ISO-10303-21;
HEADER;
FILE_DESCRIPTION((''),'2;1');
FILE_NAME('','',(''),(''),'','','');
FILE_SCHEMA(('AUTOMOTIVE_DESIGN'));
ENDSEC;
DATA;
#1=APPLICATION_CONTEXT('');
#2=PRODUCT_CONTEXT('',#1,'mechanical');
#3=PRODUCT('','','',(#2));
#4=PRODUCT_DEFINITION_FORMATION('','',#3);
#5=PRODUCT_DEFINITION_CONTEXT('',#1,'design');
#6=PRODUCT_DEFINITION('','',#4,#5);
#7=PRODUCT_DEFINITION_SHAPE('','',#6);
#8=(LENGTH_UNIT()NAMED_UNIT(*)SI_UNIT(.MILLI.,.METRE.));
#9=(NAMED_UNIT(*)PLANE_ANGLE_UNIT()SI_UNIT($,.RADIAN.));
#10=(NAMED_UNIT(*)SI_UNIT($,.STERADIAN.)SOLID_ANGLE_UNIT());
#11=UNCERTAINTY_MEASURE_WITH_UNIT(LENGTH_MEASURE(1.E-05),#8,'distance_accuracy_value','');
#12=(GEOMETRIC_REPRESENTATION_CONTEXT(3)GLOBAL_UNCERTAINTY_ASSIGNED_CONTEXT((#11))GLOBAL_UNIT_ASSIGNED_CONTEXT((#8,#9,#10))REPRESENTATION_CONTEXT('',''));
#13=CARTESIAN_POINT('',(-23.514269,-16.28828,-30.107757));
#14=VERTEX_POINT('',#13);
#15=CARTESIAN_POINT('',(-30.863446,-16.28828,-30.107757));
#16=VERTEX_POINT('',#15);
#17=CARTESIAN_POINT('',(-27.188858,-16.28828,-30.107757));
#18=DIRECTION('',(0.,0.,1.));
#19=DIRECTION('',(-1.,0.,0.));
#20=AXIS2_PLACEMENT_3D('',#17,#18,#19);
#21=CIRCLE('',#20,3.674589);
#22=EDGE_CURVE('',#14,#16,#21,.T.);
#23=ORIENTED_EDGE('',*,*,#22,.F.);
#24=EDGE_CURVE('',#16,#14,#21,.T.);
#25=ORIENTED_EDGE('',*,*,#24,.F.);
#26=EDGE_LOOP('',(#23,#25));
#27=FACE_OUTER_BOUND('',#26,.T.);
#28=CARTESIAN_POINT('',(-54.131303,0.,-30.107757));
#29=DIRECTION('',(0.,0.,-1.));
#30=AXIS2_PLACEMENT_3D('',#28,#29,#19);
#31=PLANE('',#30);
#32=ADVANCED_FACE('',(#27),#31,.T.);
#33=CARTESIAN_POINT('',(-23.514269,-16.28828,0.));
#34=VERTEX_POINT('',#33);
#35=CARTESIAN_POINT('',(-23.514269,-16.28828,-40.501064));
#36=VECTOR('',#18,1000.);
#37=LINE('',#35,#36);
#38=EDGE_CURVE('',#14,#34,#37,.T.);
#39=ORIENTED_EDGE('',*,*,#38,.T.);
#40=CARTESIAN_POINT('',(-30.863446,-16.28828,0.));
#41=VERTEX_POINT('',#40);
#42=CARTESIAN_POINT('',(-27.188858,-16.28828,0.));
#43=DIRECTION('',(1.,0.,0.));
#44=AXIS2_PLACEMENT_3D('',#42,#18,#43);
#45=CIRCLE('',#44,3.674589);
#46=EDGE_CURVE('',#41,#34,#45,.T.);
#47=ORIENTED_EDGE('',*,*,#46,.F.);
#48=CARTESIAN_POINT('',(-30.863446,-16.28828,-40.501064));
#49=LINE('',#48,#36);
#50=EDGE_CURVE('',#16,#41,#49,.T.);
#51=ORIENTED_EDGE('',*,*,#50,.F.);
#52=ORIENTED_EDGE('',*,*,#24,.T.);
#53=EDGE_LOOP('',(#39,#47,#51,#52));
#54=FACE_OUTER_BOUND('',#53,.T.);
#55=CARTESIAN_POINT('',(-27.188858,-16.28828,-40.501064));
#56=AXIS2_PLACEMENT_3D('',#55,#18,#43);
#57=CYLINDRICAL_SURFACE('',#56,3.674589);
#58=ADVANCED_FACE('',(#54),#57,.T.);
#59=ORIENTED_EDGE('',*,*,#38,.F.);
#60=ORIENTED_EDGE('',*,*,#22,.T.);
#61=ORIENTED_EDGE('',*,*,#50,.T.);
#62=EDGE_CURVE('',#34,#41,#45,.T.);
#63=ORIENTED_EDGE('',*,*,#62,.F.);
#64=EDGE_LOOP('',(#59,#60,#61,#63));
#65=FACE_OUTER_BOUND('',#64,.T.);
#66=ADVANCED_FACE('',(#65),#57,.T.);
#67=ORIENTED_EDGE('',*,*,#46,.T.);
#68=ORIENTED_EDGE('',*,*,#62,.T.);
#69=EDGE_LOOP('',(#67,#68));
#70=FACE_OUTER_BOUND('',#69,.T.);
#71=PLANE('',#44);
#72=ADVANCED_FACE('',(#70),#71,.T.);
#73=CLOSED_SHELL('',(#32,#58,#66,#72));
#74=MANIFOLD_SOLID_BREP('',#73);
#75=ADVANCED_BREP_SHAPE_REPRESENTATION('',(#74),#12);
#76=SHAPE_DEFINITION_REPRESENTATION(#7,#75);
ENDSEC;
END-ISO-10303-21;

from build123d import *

# Parameters (mm, degrees)
SKETCH1_R           = 3.674588618
BOSS_EXTRUDE1_DEPTH = 30.107757446


with BuildPart() as part:
    # Sketch1 → Boss-Extrude1 (new body)
    with BuildSketch(Plane.XY):
        with Locations((-27.188857752, -16.288280471)):
            Circle(SKETCH1_R)
    extrude(amount=-BOSS_EXTRUDE1_DEPTH)


solid = part.part
